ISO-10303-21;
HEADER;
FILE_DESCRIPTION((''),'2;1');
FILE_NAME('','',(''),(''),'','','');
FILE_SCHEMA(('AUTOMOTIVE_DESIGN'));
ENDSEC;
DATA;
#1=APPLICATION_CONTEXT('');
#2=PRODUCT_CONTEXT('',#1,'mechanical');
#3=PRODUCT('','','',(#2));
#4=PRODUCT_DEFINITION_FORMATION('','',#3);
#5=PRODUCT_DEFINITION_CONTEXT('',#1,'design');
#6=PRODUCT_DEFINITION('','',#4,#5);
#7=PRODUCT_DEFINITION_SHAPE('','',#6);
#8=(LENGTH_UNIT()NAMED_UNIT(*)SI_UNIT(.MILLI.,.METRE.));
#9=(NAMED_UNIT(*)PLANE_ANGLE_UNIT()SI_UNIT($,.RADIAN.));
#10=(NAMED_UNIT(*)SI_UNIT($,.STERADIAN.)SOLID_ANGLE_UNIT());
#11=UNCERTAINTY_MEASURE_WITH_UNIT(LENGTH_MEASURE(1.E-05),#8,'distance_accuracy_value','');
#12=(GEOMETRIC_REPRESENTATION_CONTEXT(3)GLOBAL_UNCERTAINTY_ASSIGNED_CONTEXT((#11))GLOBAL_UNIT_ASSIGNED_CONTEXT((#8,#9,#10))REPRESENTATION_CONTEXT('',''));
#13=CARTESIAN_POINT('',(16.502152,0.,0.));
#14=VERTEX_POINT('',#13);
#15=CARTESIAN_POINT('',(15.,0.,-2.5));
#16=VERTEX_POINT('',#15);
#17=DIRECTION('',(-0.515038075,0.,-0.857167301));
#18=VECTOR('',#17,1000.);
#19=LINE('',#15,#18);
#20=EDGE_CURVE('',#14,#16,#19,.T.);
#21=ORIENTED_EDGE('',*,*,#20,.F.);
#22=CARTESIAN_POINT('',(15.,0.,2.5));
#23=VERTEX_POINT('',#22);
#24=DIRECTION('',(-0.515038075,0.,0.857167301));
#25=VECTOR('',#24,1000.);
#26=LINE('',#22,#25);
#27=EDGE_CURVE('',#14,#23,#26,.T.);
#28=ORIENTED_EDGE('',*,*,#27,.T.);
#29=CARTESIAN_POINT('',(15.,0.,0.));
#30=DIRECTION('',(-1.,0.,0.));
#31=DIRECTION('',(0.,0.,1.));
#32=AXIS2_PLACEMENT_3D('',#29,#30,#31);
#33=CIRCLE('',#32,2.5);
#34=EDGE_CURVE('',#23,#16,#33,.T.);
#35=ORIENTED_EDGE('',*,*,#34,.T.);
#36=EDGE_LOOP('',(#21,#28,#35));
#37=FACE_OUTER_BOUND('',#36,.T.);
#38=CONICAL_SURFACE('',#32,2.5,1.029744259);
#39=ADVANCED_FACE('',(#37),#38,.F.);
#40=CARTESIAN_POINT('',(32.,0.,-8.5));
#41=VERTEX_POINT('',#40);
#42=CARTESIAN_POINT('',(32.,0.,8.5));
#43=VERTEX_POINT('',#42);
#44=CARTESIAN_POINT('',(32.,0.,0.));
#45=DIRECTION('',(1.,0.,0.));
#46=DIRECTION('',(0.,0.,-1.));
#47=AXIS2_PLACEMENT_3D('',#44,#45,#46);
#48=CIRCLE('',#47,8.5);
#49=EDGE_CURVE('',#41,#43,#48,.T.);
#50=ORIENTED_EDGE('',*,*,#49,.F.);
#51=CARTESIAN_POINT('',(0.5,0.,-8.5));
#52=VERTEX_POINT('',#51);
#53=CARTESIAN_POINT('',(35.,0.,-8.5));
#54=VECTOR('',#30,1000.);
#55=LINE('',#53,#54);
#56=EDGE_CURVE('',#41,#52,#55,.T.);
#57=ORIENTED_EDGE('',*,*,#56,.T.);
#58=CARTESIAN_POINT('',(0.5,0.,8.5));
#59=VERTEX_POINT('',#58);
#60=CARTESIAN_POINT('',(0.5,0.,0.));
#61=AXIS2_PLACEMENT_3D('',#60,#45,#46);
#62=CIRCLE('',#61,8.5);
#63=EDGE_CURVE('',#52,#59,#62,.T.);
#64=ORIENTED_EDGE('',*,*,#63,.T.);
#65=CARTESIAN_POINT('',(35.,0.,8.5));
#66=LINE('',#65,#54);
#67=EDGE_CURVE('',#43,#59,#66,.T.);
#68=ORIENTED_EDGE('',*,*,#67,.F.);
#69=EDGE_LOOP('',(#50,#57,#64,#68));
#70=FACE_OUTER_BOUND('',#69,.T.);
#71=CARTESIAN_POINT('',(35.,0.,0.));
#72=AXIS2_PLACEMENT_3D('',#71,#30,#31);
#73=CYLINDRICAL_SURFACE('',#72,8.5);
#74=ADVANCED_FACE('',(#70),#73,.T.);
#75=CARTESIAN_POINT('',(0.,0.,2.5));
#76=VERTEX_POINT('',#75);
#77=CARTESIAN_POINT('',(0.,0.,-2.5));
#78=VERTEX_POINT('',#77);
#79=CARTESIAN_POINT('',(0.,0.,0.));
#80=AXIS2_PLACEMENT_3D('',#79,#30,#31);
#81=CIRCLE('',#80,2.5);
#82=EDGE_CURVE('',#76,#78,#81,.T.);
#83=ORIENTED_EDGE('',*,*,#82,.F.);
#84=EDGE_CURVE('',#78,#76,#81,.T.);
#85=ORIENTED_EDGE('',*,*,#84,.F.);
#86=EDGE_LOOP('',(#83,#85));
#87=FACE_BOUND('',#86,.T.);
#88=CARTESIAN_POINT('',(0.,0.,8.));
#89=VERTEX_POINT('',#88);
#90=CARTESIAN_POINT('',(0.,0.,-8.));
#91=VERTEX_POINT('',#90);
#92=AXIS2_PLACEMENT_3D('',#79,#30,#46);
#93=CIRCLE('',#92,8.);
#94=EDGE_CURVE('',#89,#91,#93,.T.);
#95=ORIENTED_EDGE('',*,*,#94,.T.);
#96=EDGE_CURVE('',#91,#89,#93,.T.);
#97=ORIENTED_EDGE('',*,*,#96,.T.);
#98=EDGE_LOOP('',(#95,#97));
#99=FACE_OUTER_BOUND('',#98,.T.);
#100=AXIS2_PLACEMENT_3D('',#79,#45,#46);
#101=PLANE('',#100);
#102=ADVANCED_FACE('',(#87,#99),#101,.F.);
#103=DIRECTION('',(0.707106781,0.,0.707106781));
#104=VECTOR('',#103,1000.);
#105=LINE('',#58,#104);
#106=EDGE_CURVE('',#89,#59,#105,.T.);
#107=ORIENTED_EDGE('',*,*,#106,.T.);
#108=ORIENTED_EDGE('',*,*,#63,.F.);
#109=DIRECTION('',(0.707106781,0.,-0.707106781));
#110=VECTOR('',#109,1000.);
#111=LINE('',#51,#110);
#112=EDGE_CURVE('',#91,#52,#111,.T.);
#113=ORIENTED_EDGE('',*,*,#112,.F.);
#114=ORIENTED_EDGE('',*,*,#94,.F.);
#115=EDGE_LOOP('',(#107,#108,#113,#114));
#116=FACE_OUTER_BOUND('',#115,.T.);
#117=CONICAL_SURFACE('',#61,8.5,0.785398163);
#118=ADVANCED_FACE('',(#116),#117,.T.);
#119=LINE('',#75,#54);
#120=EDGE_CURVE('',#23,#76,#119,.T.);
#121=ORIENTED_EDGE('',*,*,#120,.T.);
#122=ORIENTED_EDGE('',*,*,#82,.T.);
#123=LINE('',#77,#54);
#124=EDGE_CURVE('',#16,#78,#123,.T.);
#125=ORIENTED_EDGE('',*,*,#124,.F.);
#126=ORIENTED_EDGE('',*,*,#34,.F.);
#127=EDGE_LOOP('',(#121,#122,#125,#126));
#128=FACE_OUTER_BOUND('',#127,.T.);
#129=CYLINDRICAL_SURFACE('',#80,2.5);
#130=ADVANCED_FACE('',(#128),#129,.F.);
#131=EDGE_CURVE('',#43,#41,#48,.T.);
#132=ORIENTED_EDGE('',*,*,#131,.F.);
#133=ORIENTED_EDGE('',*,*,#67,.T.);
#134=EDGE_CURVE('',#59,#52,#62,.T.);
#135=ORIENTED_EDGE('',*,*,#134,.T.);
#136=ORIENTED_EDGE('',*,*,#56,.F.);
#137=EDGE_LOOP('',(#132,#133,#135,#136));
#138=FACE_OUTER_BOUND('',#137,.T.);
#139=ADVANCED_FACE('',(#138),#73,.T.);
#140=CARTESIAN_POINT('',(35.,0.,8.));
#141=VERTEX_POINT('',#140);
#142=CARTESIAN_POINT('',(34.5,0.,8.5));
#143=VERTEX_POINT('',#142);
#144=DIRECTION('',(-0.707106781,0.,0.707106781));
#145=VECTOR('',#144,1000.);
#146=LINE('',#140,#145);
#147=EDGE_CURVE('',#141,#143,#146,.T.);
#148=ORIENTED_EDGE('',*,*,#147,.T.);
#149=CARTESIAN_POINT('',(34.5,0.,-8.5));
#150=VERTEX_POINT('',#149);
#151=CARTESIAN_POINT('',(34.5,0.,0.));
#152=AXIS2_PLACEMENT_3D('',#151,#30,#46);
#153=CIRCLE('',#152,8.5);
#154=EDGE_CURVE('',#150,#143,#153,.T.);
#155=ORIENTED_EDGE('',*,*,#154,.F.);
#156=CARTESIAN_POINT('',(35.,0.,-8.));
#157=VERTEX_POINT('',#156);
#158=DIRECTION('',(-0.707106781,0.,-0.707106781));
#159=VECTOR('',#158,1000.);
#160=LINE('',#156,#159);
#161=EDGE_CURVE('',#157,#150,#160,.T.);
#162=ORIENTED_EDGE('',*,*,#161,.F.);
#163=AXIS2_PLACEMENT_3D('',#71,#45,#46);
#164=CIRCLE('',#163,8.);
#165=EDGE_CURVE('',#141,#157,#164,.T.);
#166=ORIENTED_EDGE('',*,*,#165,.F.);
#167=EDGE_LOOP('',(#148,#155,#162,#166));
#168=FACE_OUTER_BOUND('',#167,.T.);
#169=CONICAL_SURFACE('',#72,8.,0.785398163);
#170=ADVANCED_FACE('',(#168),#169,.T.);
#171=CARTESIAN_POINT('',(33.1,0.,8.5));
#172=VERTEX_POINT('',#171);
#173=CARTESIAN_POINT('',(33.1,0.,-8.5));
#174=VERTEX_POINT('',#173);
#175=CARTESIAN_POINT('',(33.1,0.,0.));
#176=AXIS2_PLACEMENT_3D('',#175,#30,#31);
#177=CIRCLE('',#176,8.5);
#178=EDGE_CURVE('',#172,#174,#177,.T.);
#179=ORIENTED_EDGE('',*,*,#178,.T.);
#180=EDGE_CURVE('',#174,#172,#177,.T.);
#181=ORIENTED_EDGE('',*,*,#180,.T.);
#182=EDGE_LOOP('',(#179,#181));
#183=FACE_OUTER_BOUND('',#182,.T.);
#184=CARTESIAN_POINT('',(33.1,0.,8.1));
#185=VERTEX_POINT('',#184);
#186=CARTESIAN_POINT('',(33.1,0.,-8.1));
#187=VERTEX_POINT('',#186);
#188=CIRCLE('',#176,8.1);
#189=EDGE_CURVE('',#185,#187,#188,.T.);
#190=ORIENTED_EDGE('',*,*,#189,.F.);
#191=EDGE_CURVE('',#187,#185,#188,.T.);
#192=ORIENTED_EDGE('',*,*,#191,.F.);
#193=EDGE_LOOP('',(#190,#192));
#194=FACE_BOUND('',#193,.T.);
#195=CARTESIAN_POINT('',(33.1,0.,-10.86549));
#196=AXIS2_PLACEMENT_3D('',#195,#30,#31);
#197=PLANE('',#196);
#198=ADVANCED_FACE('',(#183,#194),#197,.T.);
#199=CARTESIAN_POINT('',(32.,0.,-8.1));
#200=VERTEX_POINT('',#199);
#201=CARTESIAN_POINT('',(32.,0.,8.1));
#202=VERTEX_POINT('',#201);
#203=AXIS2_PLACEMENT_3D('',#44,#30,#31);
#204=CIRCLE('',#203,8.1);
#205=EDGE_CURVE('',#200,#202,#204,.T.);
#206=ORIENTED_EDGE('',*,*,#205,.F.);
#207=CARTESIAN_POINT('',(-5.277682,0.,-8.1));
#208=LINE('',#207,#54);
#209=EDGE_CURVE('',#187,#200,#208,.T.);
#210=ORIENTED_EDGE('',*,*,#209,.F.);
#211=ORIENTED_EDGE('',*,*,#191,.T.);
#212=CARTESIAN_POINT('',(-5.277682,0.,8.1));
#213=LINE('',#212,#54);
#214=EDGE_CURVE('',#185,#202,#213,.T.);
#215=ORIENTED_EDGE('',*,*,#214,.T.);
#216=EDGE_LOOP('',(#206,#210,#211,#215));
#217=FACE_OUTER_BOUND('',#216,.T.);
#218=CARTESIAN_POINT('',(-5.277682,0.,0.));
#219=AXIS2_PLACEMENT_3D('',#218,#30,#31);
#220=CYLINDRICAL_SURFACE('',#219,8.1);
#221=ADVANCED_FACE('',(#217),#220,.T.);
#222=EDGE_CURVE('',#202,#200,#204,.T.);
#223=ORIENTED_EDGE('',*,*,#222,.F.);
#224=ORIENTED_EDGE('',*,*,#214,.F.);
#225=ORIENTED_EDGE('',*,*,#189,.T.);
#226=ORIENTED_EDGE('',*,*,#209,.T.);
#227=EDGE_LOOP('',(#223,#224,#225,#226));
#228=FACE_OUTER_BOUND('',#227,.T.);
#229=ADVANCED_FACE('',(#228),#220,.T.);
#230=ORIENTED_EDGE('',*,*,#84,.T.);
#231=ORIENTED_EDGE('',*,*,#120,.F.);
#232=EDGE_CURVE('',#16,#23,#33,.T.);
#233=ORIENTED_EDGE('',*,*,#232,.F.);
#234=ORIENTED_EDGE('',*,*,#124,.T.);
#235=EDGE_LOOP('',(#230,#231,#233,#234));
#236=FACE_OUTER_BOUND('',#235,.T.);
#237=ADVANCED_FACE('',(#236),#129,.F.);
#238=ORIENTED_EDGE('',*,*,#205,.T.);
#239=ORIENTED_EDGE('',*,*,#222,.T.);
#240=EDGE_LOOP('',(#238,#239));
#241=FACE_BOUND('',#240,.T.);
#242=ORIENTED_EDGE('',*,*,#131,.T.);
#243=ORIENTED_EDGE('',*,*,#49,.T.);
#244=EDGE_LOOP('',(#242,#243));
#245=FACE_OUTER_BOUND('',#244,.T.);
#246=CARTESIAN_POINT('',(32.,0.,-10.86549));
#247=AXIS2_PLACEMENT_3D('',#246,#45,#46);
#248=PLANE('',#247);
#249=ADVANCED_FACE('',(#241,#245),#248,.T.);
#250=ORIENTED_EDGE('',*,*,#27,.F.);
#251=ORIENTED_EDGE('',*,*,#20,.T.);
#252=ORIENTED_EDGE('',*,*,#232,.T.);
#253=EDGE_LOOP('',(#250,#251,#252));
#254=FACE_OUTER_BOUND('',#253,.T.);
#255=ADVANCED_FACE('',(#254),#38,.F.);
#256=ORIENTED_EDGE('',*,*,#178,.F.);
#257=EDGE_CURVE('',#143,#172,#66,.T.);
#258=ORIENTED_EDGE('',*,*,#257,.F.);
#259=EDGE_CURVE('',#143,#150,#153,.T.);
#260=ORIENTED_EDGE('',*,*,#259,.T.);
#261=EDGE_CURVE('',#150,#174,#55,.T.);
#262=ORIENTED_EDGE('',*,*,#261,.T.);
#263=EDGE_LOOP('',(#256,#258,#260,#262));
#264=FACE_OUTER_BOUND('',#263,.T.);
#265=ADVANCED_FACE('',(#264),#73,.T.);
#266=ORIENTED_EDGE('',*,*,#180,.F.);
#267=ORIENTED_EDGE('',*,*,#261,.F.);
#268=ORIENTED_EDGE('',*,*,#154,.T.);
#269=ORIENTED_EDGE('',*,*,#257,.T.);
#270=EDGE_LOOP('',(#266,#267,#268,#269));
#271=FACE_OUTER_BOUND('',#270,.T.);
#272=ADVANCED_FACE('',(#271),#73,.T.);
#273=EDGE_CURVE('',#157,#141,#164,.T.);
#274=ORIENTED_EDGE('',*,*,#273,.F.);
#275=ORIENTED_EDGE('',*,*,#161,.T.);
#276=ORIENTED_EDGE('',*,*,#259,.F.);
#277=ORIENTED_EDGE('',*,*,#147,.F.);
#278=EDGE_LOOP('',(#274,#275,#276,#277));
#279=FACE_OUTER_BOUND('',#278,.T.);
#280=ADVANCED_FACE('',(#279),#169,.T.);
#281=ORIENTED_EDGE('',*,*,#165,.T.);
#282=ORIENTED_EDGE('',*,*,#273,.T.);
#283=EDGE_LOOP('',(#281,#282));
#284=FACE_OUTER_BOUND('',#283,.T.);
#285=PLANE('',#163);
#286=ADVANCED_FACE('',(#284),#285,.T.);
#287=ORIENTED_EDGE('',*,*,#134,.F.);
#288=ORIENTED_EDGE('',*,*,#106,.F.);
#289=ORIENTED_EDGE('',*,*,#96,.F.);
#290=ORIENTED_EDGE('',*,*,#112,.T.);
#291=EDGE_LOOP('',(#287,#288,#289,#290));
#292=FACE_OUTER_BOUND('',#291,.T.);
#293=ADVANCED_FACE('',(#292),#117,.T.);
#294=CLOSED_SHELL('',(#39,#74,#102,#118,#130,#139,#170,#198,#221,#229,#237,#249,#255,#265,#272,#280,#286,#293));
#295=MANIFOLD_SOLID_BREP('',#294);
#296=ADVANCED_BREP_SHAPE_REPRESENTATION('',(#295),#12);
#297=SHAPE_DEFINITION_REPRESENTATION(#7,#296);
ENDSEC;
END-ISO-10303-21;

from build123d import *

# Parameters (mm, degrees)
SKETCH_1_R             = 8.5
EXTRUDE_1_DEPTH        = 35
HOLE_WIZARD_M6_1_D     = 5
HOLE_WIZARD_M6_1_DEPTH = 15
HOLE_WIZARD_M6_1_TIP   = 1.502151548
CHAMFER_1_SIZE         = 0.5
SKETCH_4_W             = 1.1
SKETCH_4_H             = 2.765489895


with BuildPart() as part:
    # 草图1 → 凸台-拉伸1 (new body)
    with BuildSketch(Plane(origin=(0, 0, 0), x_dir=(0, 0, -1), z_dir=(1, 0, 0))):
        Circle(SKETCH_1_R)
    extrude(amount=EXTRUDE_1_DEPTH)

    # M6 螺纹孔1
    with Locations(Plane.ZY):
        with Locations((0, 0)):
            Hole(HOLE_WIZARD_M6_1_D / 2, depth=HOLE_WIZARD_M6_1_DEPTH)
            with Locations((0, 0, -(HOLE_WIZARD_M6_1_DEPTH + HOLE_WIZARD_M6_1_TIP / 2))):  # 118° drill point
                Cone(0, HOLE_WIZARD_M6_1_D / 2, HOLE_WIZARD_M6_1_TIP, mode=Mode.SUBTRACT)

    # 倒角1
    chamfer_1_edges = [part.edges().sort_by_distance(p)[0] for p in [
        (0, 0, 8.5),
        (35, 0, 8.5),
    ]]
    chamfer(chamfer_1_edges, length=CHAMFER_1_SIZE)

    # 草图4 → 切除-旋转1 (revolve, cut)
    with BuildSketch(Plane(origin=(0, 0, 0), x_dir=(1, 0, 0), z_dir=(0, 1, 0)), mode=Mode.PRIVATE) as cut_revolve_1_sk:
        with Locations((32.55, 9.482744948)):
            Rectangle(SKETCH_4_W, SKETCH_4_H)
    revolve(cut_revolve_1_sk.sketch.rotate(Axis((-5.277682127, 0, 0), (1, 0, 0)), 180), axis=Axis((-5.277682127, 0, 0), (1, 0, 0)), mode=Mode.SUBTRACT)


solid = part.part
